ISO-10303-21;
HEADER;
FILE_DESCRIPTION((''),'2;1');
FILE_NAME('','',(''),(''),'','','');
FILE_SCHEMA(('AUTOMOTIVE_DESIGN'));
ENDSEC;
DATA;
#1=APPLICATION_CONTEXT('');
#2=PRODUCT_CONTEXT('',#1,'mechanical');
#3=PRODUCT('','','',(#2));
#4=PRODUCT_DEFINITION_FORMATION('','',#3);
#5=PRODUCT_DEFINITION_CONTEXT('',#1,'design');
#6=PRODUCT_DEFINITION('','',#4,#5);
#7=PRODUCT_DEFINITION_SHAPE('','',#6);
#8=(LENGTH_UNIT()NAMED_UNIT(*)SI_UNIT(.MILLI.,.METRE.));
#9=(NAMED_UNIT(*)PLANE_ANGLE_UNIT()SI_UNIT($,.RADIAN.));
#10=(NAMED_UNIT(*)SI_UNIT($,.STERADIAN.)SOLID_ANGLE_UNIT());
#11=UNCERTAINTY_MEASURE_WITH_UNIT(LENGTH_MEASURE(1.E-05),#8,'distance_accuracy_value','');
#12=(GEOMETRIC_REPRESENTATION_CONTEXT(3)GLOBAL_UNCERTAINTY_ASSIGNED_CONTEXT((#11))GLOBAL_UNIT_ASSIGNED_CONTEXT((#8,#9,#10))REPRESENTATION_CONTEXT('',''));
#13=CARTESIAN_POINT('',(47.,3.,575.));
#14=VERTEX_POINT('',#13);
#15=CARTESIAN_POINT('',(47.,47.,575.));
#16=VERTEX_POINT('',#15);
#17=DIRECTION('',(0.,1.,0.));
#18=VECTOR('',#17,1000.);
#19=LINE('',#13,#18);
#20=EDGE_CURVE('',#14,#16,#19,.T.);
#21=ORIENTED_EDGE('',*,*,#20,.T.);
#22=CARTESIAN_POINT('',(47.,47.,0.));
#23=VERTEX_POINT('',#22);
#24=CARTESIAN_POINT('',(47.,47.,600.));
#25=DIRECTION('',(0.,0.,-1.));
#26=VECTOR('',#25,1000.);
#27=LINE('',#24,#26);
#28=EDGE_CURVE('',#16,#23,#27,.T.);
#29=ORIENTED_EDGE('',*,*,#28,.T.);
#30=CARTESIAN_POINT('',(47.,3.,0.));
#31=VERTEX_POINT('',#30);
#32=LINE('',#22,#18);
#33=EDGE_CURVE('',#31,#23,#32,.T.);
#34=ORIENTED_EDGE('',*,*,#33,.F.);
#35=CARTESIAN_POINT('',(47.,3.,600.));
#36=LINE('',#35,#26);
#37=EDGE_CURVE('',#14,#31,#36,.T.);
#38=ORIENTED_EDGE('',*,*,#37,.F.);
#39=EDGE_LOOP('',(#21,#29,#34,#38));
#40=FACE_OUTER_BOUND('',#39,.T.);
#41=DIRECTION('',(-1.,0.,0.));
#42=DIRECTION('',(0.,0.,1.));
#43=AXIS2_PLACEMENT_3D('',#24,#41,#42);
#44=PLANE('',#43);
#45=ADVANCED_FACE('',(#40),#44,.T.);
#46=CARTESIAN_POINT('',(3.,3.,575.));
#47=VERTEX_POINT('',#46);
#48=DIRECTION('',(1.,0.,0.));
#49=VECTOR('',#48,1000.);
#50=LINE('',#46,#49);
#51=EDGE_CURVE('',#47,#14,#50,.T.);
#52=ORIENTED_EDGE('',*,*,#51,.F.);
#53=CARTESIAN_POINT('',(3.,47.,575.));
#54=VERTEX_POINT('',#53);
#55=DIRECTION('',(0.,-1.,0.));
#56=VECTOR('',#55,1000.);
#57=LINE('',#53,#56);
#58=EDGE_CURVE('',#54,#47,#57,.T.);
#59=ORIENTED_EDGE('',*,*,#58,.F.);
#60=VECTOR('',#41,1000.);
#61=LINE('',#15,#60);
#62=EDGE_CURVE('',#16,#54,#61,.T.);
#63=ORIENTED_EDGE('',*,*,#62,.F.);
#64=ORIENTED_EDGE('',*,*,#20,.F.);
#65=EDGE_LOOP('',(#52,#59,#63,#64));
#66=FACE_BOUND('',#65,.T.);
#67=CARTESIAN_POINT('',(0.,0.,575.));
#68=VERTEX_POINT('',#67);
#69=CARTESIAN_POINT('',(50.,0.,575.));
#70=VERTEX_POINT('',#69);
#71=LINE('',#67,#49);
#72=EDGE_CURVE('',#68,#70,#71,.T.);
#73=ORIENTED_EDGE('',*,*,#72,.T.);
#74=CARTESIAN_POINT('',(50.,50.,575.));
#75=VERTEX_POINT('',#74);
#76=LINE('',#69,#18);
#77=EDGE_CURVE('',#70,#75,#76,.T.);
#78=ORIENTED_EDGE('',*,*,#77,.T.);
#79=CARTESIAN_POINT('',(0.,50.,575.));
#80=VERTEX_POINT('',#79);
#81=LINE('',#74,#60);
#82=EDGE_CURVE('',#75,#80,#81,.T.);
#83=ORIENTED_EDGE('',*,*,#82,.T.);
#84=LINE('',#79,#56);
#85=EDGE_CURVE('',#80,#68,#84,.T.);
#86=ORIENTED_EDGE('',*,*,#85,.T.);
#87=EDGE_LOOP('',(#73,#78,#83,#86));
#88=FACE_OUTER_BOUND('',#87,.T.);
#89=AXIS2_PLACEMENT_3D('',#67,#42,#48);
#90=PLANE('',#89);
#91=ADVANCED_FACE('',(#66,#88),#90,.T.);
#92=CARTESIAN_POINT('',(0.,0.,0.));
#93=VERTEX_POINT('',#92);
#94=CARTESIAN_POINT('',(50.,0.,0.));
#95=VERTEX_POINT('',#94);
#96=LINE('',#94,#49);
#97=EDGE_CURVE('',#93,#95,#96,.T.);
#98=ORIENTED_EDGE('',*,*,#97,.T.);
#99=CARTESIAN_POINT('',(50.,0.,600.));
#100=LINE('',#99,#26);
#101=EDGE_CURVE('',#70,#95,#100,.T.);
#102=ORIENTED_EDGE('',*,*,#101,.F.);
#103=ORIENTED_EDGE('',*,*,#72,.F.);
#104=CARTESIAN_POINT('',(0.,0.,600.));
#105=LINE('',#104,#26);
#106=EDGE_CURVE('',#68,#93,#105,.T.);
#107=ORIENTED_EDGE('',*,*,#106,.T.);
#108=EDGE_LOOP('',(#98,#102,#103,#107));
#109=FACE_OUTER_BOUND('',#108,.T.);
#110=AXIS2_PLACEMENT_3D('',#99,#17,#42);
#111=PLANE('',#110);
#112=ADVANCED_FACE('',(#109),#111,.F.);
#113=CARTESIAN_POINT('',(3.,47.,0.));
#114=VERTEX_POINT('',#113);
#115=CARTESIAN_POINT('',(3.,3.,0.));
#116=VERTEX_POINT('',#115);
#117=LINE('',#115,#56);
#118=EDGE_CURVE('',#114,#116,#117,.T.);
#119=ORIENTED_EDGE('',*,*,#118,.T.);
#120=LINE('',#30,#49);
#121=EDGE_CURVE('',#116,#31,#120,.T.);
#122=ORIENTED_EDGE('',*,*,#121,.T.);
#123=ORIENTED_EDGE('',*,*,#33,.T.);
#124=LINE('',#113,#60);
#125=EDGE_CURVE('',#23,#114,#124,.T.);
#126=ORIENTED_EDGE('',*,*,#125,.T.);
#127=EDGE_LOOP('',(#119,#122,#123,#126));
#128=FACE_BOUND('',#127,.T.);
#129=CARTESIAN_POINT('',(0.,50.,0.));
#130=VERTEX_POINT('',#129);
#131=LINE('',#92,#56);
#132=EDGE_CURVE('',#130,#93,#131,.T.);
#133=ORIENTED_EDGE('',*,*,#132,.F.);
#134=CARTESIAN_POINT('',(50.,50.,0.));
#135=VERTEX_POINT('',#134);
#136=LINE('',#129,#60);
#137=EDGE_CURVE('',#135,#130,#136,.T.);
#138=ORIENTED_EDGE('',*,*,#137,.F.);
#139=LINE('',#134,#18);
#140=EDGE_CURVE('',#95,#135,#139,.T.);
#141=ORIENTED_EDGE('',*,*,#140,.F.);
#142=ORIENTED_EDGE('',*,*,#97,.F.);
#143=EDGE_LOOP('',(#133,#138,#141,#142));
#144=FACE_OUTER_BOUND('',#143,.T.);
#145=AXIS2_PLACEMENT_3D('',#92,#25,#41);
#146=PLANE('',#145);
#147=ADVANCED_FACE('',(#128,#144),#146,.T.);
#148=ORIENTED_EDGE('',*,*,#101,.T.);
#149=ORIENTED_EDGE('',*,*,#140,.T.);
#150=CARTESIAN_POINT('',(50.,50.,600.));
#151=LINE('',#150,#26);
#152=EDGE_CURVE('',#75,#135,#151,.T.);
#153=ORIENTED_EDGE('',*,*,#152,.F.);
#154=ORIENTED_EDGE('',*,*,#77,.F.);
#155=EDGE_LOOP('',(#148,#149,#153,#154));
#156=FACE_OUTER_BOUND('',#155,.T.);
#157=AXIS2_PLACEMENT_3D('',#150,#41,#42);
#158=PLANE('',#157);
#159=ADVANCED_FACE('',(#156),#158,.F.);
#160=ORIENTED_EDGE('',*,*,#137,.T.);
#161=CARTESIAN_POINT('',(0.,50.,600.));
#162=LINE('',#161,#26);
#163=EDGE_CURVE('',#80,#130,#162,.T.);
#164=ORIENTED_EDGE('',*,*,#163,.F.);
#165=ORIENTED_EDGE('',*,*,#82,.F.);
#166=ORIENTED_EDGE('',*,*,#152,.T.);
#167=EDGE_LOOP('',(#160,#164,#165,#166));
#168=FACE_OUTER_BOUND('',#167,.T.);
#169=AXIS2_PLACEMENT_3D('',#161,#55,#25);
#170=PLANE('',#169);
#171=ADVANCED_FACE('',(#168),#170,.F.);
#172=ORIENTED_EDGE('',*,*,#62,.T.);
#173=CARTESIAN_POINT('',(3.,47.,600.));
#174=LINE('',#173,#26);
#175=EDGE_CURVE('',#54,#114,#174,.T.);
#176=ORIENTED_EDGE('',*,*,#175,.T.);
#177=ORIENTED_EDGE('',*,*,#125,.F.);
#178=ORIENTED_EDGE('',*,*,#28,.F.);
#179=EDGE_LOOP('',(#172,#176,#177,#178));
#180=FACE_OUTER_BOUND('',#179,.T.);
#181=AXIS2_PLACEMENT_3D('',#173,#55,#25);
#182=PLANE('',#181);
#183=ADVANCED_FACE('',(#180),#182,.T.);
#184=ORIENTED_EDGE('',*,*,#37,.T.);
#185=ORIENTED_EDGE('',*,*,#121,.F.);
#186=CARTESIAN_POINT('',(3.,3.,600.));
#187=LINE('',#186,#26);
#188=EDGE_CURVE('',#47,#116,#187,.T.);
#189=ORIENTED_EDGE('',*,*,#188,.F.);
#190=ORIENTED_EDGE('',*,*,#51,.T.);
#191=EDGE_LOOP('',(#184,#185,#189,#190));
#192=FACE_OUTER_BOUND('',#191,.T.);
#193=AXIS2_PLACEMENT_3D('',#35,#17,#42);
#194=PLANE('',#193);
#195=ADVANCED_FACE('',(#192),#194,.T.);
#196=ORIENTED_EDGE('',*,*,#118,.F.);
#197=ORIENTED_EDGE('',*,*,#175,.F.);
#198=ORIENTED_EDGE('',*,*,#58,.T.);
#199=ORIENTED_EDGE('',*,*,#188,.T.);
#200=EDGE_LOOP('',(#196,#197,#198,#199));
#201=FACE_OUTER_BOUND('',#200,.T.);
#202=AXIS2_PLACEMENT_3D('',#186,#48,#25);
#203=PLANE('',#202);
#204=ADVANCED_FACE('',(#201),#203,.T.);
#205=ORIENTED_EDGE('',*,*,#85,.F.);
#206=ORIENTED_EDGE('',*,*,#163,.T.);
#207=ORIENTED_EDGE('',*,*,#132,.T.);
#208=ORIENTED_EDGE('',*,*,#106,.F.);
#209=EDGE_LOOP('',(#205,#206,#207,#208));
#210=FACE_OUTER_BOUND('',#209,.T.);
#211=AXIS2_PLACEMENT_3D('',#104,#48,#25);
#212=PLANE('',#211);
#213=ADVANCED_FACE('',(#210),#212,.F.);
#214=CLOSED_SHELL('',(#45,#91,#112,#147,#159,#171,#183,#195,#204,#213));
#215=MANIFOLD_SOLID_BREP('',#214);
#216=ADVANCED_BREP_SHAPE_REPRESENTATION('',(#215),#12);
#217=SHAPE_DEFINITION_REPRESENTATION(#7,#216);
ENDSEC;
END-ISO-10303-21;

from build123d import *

# Parameters (mm, degrees)
SKETCH_1_W          = 50
SKETCH_1_H          = 50
SKETCH_1_W_2        = 44
SKETCH_1_H_2        = 44
EXTRUDE_1_DEPTH     = 600
SKETCH_2_W          = 50
SKETCH_2_H          = 50
SKETCH_2_W_2        = 44
SKETCH_2_H_2        = 44
CUT_EXTRUDE_1_DEPTH = 25


with BuildPart() as part:
    # 草图1 → 凸台-拉伸1 (new body)
    with BuildSketch(Plane.XY):
        with Locations((25, 25)):
            Rectangle(SKETCH_1_W, SKETCH_1_H)
        with Locations((25, 25)):
            Rectangle(SKETCH_1_W_2, SKETCH_1_H_2, mode=Mode.SUBTRACT)
    extrude(amount=EXTRUDE_1_DEPTH)

    # 草图2 → 切除-拉伸1 (cut)
    with BuildSketch(Plane.XY.offset(600)):
        with Locations((25, 25)):
            Rectangle(SKETCH_2_W, SKETCH_2_H)
        with Locations((25, 25)):
            Rectangle(SKETCH_2_W_2, SKETCH_2_H_2, mode=Mode.SUBTRACT)
    extrude(amount=-CUT_EXTRUDE_1_DEPTH, mode=Mode.SUBTRACT)


solid = part.part
